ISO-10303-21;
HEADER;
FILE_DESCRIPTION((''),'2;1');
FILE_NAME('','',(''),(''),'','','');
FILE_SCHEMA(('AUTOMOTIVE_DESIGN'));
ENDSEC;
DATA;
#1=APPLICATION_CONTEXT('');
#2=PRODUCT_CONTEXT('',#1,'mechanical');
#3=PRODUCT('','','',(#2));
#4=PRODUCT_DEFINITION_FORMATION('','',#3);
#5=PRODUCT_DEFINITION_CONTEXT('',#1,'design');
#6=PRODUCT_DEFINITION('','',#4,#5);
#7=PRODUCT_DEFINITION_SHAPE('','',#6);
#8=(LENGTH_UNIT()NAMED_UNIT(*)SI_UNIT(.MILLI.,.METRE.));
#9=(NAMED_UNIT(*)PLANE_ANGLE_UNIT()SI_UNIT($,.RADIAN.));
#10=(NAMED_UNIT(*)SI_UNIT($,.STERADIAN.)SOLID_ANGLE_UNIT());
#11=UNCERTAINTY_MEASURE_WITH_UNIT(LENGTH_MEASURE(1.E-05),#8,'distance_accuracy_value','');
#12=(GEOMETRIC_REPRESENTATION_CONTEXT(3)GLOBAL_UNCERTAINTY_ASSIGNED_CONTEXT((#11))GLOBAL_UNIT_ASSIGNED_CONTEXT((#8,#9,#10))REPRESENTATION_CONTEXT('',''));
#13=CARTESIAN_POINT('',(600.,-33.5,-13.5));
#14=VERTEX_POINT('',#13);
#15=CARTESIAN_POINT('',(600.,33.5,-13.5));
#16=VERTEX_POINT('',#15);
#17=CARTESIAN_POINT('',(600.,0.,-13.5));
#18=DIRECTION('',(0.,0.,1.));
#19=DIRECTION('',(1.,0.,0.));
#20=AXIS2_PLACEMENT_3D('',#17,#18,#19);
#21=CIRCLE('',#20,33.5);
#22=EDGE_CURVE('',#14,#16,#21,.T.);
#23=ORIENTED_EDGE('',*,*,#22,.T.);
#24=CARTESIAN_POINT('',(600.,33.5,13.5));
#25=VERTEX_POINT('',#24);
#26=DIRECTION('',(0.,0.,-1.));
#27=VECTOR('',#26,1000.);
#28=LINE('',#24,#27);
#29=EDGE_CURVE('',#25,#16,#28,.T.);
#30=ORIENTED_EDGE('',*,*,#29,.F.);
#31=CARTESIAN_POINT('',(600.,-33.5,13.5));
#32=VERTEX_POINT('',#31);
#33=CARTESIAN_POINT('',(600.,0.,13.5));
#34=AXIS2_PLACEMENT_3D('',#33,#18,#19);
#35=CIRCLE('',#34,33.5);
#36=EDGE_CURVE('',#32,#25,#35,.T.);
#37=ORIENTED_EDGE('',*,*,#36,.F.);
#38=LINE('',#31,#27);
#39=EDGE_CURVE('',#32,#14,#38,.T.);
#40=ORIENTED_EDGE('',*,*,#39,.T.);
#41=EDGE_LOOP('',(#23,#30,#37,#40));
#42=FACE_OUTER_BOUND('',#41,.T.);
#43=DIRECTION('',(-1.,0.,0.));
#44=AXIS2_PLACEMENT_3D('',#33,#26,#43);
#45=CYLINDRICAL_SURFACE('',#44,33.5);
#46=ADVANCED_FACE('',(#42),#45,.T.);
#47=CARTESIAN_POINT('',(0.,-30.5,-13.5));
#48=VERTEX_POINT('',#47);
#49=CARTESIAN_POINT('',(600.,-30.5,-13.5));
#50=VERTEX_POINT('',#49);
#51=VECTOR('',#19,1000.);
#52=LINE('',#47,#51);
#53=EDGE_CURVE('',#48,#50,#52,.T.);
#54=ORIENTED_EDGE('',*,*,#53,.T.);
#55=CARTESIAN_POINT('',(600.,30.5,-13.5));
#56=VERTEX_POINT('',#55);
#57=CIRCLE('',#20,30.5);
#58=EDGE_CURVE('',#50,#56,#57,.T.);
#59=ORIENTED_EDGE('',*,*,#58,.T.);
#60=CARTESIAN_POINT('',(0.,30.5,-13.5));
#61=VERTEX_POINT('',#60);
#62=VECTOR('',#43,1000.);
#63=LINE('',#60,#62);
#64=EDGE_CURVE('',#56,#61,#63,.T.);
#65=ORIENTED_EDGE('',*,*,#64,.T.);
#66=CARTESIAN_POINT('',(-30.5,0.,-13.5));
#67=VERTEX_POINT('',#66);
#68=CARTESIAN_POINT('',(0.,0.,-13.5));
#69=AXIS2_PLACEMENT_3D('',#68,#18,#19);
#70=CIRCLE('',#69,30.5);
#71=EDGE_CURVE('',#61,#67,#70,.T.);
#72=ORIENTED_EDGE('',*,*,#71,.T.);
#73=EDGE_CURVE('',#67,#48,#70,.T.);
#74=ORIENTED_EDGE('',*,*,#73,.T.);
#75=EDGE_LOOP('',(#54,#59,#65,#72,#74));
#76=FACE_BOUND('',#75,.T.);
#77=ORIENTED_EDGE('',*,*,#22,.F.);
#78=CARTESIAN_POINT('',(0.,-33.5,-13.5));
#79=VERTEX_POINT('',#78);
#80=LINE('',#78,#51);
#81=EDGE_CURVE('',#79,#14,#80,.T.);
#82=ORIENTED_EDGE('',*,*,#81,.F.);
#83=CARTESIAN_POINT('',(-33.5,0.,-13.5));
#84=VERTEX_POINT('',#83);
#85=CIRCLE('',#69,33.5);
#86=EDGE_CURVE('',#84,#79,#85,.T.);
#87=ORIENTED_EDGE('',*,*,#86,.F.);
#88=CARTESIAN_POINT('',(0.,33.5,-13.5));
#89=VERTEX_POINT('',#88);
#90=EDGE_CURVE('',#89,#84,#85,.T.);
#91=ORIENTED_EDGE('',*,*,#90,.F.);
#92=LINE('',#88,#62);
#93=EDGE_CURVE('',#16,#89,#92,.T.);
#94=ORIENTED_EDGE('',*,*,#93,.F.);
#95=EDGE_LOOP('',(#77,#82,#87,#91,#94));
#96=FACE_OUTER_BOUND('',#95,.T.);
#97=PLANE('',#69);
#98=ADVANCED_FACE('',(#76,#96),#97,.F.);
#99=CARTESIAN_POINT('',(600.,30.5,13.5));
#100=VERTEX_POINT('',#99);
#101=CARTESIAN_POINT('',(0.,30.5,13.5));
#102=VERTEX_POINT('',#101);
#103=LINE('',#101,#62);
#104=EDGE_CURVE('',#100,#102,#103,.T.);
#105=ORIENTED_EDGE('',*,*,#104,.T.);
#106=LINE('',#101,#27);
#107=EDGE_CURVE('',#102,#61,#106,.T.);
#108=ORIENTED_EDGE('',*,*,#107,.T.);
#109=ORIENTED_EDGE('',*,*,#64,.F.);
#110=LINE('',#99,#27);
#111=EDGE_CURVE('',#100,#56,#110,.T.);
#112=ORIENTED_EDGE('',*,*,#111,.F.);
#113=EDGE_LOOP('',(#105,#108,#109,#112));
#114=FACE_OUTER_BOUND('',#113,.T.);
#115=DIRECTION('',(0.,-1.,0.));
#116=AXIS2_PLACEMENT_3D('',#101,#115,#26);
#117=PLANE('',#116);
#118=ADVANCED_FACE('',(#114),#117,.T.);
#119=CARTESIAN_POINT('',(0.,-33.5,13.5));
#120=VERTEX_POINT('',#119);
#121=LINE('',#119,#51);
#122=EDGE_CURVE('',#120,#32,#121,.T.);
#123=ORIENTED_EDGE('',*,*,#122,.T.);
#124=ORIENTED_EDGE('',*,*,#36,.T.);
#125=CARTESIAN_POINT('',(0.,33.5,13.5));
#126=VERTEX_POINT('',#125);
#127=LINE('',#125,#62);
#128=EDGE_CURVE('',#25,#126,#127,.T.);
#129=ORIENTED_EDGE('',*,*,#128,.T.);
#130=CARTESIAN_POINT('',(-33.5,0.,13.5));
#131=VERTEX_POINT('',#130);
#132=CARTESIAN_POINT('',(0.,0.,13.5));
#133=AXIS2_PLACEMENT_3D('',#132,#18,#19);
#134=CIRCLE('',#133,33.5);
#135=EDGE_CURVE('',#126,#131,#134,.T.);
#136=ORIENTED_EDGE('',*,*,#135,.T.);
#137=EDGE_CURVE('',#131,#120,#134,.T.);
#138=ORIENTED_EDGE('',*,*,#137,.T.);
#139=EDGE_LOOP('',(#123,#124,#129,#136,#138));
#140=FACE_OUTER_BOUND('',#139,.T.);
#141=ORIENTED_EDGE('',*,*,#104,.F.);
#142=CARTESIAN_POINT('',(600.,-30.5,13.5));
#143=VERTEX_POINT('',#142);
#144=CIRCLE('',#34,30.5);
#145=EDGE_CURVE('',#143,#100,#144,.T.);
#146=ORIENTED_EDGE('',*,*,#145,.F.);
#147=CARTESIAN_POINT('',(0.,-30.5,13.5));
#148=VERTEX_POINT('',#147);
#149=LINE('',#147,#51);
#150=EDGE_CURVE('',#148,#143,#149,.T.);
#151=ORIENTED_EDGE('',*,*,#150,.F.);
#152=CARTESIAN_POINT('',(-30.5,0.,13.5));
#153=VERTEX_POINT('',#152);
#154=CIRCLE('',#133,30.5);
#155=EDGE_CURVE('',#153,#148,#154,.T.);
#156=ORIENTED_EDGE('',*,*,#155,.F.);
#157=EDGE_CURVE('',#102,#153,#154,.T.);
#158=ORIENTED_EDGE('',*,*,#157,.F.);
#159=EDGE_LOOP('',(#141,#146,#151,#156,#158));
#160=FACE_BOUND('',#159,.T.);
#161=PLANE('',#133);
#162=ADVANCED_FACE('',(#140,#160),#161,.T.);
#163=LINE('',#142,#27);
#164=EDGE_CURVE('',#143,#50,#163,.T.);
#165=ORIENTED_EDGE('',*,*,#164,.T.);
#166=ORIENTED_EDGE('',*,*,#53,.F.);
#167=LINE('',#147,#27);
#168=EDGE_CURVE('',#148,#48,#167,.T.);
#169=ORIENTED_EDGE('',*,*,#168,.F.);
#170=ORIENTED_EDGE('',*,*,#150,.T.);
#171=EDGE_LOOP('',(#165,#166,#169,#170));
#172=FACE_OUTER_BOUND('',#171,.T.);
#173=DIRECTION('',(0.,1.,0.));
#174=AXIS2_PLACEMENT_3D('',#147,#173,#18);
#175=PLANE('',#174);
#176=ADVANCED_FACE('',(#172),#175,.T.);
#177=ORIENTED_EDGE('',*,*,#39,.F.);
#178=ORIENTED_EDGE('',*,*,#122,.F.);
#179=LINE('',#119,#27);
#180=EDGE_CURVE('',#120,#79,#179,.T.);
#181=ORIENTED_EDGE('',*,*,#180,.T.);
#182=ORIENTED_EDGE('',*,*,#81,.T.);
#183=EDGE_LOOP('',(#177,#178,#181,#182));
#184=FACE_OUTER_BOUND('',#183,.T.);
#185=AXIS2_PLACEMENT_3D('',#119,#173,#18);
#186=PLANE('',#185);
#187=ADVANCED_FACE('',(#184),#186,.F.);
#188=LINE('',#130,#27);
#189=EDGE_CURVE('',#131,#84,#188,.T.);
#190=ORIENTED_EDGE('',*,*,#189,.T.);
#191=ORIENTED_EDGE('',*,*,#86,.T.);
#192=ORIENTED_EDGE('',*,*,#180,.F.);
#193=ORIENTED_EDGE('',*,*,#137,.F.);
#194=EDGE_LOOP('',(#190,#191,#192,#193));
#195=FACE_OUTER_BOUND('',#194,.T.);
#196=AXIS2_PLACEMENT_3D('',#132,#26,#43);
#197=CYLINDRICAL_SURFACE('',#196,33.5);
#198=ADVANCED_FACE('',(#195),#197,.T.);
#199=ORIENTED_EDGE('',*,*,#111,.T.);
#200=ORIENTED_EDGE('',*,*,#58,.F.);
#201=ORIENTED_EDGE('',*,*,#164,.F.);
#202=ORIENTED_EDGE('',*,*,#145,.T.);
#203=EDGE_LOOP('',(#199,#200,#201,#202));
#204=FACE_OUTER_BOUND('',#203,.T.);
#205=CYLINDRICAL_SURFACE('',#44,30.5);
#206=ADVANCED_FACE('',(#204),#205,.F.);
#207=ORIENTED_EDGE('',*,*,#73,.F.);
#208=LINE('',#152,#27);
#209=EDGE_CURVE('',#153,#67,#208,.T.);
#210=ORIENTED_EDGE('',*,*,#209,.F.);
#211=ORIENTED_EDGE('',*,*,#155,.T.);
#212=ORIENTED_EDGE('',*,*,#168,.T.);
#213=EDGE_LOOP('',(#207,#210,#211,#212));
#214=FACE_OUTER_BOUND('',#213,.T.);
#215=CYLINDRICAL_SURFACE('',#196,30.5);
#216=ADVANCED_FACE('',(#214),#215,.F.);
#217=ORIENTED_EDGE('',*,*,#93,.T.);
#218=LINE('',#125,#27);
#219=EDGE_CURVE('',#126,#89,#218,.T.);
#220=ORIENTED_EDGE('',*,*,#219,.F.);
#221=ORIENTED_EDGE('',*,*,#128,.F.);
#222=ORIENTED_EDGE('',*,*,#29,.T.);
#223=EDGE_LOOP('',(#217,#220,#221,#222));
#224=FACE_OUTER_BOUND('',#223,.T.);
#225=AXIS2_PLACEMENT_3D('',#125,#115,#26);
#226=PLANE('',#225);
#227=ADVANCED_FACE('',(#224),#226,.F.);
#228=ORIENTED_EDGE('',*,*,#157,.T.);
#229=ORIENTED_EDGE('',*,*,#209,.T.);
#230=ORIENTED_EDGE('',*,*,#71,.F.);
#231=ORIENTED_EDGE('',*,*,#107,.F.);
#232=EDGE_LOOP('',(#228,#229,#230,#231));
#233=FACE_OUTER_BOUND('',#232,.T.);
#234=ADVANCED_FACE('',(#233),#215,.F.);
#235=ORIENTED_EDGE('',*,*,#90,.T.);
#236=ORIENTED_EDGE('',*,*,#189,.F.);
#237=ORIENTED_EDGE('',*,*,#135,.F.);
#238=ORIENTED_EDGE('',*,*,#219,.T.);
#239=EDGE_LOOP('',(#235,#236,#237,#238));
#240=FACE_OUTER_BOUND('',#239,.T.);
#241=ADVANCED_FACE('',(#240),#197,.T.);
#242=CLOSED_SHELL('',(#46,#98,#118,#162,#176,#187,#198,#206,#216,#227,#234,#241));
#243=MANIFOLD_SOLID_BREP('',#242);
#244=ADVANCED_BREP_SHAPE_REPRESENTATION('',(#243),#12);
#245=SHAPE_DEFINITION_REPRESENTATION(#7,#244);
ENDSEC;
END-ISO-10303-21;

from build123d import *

# Parameters (mm, degrees)
BOSS_EXTRUDE1_DEPTH = 13.5


with BuildPart() as part:
    # Sketch1 → Boss-Extrude1 (new, symmetric)
    with BuildSketch(Plane.XY):
        with BuildLine():
            Line((0, 33.5), (600, 33.5))
            ThreePointArc((600, 33.5), (633.5, 0), (600, -33.5))
            Line((600, -33.5), (0, -33.5))
            ThreePointArc((0, -33.5), (-33.5, 0), (0, 33.5))
        make_face()
        with BuildLine():
            Line((0, 30.5), (600, 30.5))
            ThreePointArc((600, 30.5), (630.5, 0), (600, -30.5))
            Line((600, -30.5), (0, -30.5))
            ThreePointArc((0, -30.5), (-30.5, 0), (0, 30.5))
        make_face(mode=Mode.SUBTRACT)
    extrude(amount=BOSS_EXTRUDE1_DEPTH, both=True)


solid = part.part
